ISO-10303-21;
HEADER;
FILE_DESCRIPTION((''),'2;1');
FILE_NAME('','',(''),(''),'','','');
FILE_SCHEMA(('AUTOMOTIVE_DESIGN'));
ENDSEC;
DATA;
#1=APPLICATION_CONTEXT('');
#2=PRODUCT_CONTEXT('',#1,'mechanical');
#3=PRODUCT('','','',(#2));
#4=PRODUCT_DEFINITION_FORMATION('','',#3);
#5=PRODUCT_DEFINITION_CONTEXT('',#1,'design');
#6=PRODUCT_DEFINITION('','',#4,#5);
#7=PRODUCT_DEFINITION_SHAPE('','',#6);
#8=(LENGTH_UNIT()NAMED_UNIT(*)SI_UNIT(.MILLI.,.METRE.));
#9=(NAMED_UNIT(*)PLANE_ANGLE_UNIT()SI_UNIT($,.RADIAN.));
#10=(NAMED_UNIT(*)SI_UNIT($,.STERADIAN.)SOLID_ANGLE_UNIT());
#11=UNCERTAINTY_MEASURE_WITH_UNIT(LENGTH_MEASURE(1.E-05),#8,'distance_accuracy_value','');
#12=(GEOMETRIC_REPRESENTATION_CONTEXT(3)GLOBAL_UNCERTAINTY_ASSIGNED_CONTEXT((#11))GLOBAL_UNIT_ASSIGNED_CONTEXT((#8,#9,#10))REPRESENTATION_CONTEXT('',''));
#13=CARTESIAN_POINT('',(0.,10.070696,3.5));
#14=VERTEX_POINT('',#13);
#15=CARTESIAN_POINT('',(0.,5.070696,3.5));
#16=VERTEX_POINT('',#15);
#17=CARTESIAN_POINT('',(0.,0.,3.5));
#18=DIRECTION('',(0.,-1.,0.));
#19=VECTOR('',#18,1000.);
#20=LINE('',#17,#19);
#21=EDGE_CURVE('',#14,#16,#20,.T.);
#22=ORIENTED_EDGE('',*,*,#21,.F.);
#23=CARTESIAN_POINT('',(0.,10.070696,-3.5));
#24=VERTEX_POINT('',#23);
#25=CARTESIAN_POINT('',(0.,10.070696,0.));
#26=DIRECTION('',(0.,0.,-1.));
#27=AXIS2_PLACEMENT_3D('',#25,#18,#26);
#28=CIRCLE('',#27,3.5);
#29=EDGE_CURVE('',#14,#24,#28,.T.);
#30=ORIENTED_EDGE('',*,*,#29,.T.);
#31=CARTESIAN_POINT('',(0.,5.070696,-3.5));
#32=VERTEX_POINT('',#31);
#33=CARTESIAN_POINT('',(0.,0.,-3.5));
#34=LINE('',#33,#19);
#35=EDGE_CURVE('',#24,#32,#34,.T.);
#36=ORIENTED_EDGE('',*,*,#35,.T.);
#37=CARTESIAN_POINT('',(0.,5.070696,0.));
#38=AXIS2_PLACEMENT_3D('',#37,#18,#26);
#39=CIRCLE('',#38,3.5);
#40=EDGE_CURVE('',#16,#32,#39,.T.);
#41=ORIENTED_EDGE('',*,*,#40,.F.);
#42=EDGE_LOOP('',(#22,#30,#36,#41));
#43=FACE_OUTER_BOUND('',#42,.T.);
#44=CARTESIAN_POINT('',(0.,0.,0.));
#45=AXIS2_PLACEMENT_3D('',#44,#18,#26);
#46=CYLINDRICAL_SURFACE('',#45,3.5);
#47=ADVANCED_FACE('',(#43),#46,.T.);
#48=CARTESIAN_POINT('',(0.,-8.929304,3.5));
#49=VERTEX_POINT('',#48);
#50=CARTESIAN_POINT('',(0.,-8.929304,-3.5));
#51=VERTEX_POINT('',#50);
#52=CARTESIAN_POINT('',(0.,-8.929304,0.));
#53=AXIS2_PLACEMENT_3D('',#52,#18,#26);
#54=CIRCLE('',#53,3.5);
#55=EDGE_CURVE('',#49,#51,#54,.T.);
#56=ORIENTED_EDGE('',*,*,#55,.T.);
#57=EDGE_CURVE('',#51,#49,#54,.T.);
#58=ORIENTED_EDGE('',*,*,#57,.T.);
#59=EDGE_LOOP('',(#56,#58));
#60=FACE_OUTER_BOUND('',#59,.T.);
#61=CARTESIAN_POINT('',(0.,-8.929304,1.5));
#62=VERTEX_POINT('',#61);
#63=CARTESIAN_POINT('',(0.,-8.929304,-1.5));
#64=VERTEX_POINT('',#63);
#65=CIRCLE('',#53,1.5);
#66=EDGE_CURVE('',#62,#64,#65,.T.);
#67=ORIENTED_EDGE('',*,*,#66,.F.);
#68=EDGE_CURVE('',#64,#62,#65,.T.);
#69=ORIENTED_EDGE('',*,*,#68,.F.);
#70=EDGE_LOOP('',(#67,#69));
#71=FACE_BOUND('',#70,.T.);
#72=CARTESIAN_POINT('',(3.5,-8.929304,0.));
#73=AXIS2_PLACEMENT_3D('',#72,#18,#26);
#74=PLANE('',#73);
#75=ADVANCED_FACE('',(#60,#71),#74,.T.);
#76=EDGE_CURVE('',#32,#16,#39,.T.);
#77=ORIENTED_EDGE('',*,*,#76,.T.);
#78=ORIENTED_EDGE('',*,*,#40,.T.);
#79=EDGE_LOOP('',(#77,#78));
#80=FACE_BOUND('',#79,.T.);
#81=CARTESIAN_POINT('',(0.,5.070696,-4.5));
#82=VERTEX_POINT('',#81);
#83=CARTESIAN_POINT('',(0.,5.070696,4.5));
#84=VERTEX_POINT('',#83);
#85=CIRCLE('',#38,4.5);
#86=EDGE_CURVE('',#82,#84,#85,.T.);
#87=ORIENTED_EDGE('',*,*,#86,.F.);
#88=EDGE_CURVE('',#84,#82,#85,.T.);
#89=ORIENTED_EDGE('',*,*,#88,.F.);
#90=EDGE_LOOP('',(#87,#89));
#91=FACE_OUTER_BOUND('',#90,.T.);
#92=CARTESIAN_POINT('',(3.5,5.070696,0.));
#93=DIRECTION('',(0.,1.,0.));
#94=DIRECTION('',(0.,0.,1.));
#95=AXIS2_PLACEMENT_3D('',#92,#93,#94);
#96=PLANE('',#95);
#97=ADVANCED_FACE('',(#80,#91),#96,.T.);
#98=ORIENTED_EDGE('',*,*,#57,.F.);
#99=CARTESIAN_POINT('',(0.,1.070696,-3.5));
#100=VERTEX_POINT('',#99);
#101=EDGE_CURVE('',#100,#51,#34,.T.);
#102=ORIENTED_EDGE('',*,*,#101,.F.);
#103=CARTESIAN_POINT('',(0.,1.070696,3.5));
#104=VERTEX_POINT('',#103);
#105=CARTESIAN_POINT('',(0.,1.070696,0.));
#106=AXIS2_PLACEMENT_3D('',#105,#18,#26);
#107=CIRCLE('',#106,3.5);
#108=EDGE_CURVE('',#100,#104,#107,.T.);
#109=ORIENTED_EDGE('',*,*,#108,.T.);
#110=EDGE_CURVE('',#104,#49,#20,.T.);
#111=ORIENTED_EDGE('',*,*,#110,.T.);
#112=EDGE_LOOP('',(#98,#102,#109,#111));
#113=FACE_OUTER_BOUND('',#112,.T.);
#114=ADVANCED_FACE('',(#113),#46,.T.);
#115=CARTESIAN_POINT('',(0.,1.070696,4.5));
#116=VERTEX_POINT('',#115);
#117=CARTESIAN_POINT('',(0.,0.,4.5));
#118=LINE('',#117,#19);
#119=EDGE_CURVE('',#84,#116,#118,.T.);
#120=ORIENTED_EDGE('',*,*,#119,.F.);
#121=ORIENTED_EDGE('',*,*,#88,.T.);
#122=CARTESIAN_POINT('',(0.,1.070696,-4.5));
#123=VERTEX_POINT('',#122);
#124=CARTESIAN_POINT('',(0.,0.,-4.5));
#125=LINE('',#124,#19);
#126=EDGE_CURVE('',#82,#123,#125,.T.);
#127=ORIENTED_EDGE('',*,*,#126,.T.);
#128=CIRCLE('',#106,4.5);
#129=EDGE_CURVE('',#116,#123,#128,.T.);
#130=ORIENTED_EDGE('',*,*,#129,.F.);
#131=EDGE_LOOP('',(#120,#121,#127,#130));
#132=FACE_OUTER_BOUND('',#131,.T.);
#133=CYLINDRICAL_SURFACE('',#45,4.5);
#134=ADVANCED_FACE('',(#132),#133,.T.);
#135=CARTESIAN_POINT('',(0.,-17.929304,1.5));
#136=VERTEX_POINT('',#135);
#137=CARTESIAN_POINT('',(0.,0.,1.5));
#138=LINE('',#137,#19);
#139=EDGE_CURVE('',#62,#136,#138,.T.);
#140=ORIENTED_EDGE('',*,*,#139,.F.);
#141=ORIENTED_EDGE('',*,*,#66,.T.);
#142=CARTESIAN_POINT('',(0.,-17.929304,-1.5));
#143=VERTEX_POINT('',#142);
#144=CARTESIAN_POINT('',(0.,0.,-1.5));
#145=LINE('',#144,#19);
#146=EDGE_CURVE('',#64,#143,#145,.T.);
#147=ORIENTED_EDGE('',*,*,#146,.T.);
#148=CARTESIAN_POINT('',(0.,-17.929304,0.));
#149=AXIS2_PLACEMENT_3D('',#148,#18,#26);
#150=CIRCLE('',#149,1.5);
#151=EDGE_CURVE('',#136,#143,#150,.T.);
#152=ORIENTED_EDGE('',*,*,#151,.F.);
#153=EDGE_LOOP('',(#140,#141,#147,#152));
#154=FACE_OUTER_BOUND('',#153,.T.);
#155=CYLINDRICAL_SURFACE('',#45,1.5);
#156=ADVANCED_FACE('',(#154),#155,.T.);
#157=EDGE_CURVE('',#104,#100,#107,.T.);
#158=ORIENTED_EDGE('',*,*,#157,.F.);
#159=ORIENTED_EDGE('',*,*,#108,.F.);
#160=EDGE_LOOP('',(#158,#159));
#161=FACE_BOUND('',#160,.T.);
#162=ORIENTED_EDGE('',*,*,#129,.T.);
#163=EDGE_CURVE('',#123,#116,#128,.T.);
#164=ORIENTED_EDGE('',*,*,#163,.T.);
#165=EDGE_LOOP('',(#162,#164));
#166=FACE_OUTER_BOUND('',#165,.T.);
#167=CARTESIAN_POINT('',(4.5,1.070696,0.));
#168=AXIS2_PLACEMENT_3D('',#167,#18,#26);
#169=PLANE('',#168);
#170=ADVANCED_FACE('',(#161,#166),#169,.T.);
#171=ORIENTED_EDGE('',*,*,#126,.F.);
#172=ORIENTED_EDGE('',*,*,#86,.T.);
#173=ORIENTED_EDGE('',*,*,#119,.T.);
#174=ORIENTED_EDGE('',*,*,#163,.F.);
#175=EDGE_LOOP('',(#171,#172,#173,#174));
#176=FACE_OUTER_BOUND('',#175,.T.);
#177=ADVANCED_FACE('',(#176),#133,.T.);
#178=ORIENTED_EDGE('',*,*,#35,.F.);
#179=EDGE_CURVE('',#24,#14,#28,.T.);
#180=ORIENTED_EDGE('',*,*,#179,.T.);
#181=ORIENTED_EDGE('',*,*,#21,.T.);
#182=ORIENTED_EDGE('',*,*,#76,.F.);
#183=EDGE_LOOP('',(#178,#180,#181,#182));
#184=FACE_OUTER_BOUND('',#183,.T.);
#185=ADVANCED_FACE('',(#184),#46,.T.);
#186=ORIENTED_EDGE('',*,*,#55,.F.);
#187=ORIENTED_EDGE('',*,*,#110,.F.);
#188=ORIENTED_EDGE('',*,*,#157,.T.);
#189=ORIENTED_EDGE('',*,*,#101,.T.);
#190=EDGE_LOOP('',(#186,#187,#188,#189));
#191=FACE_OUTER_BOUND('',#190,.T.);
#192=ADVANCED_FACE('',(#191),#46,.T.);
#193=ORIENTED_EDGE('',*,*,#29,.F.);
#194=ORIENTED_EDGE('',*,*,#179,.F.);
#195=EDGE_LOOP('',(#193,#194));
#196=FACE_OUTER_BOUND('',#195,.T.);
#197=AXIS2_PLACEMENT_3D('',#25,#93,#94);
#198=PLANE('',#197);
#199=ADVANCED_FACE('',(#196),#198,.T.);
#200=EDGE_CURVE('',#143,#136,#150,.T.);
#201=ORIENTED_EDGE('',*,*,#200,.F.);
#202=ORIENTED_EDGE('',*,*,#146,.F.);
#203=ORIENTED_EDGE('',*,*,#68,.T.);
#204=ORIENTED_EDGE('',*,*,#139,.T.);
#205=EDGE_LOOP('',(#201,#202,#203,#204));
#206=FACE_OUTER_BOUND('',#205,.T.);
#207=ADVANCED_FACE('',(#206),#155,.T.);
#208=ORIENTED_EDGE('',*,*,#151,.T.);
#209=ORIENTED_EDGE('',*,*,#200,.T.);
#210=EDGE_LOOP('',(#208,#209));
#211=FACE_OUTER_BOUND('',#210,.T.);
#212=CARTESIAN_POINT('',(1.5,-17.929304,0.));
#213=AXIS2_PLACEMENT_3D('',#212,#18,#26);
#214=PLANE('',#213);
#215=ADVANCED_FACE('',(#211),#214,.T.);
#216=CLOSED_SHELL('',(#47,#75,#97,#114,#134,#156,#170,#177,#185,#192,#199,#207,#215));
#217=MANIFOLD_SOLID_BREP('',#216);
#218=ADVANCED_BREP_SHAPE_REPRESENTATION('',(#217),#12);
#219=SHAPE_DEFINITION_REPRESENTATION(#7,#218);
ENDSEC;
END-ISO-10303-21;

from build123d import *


with BuildPart() as part:
    # 草图3 → 旋转19 (revolve)
    with BuildSketch(Plane.XY, mode=Mode.PRIVATE) as revolve_19_sk:
        Polygon((0, 10.070696149), (3.5, 10.070696149), (3.5, 5.070696149), (4.5, 5.070696149), (4.5, 1.070696149), (3.5, 1.070696149), (3.5, -8.929303851), (1.5, -8.929303851), (1.5, -17.929303851), (0, -17.929303851), align=None)
    revolve(revolve_19_sk.sketch.rotate(Axis((0, 0, 0), (0, 1, 0)), 90), axis=Axis((0, 0, 0), (0, 1, 0)))


solid = part.part
